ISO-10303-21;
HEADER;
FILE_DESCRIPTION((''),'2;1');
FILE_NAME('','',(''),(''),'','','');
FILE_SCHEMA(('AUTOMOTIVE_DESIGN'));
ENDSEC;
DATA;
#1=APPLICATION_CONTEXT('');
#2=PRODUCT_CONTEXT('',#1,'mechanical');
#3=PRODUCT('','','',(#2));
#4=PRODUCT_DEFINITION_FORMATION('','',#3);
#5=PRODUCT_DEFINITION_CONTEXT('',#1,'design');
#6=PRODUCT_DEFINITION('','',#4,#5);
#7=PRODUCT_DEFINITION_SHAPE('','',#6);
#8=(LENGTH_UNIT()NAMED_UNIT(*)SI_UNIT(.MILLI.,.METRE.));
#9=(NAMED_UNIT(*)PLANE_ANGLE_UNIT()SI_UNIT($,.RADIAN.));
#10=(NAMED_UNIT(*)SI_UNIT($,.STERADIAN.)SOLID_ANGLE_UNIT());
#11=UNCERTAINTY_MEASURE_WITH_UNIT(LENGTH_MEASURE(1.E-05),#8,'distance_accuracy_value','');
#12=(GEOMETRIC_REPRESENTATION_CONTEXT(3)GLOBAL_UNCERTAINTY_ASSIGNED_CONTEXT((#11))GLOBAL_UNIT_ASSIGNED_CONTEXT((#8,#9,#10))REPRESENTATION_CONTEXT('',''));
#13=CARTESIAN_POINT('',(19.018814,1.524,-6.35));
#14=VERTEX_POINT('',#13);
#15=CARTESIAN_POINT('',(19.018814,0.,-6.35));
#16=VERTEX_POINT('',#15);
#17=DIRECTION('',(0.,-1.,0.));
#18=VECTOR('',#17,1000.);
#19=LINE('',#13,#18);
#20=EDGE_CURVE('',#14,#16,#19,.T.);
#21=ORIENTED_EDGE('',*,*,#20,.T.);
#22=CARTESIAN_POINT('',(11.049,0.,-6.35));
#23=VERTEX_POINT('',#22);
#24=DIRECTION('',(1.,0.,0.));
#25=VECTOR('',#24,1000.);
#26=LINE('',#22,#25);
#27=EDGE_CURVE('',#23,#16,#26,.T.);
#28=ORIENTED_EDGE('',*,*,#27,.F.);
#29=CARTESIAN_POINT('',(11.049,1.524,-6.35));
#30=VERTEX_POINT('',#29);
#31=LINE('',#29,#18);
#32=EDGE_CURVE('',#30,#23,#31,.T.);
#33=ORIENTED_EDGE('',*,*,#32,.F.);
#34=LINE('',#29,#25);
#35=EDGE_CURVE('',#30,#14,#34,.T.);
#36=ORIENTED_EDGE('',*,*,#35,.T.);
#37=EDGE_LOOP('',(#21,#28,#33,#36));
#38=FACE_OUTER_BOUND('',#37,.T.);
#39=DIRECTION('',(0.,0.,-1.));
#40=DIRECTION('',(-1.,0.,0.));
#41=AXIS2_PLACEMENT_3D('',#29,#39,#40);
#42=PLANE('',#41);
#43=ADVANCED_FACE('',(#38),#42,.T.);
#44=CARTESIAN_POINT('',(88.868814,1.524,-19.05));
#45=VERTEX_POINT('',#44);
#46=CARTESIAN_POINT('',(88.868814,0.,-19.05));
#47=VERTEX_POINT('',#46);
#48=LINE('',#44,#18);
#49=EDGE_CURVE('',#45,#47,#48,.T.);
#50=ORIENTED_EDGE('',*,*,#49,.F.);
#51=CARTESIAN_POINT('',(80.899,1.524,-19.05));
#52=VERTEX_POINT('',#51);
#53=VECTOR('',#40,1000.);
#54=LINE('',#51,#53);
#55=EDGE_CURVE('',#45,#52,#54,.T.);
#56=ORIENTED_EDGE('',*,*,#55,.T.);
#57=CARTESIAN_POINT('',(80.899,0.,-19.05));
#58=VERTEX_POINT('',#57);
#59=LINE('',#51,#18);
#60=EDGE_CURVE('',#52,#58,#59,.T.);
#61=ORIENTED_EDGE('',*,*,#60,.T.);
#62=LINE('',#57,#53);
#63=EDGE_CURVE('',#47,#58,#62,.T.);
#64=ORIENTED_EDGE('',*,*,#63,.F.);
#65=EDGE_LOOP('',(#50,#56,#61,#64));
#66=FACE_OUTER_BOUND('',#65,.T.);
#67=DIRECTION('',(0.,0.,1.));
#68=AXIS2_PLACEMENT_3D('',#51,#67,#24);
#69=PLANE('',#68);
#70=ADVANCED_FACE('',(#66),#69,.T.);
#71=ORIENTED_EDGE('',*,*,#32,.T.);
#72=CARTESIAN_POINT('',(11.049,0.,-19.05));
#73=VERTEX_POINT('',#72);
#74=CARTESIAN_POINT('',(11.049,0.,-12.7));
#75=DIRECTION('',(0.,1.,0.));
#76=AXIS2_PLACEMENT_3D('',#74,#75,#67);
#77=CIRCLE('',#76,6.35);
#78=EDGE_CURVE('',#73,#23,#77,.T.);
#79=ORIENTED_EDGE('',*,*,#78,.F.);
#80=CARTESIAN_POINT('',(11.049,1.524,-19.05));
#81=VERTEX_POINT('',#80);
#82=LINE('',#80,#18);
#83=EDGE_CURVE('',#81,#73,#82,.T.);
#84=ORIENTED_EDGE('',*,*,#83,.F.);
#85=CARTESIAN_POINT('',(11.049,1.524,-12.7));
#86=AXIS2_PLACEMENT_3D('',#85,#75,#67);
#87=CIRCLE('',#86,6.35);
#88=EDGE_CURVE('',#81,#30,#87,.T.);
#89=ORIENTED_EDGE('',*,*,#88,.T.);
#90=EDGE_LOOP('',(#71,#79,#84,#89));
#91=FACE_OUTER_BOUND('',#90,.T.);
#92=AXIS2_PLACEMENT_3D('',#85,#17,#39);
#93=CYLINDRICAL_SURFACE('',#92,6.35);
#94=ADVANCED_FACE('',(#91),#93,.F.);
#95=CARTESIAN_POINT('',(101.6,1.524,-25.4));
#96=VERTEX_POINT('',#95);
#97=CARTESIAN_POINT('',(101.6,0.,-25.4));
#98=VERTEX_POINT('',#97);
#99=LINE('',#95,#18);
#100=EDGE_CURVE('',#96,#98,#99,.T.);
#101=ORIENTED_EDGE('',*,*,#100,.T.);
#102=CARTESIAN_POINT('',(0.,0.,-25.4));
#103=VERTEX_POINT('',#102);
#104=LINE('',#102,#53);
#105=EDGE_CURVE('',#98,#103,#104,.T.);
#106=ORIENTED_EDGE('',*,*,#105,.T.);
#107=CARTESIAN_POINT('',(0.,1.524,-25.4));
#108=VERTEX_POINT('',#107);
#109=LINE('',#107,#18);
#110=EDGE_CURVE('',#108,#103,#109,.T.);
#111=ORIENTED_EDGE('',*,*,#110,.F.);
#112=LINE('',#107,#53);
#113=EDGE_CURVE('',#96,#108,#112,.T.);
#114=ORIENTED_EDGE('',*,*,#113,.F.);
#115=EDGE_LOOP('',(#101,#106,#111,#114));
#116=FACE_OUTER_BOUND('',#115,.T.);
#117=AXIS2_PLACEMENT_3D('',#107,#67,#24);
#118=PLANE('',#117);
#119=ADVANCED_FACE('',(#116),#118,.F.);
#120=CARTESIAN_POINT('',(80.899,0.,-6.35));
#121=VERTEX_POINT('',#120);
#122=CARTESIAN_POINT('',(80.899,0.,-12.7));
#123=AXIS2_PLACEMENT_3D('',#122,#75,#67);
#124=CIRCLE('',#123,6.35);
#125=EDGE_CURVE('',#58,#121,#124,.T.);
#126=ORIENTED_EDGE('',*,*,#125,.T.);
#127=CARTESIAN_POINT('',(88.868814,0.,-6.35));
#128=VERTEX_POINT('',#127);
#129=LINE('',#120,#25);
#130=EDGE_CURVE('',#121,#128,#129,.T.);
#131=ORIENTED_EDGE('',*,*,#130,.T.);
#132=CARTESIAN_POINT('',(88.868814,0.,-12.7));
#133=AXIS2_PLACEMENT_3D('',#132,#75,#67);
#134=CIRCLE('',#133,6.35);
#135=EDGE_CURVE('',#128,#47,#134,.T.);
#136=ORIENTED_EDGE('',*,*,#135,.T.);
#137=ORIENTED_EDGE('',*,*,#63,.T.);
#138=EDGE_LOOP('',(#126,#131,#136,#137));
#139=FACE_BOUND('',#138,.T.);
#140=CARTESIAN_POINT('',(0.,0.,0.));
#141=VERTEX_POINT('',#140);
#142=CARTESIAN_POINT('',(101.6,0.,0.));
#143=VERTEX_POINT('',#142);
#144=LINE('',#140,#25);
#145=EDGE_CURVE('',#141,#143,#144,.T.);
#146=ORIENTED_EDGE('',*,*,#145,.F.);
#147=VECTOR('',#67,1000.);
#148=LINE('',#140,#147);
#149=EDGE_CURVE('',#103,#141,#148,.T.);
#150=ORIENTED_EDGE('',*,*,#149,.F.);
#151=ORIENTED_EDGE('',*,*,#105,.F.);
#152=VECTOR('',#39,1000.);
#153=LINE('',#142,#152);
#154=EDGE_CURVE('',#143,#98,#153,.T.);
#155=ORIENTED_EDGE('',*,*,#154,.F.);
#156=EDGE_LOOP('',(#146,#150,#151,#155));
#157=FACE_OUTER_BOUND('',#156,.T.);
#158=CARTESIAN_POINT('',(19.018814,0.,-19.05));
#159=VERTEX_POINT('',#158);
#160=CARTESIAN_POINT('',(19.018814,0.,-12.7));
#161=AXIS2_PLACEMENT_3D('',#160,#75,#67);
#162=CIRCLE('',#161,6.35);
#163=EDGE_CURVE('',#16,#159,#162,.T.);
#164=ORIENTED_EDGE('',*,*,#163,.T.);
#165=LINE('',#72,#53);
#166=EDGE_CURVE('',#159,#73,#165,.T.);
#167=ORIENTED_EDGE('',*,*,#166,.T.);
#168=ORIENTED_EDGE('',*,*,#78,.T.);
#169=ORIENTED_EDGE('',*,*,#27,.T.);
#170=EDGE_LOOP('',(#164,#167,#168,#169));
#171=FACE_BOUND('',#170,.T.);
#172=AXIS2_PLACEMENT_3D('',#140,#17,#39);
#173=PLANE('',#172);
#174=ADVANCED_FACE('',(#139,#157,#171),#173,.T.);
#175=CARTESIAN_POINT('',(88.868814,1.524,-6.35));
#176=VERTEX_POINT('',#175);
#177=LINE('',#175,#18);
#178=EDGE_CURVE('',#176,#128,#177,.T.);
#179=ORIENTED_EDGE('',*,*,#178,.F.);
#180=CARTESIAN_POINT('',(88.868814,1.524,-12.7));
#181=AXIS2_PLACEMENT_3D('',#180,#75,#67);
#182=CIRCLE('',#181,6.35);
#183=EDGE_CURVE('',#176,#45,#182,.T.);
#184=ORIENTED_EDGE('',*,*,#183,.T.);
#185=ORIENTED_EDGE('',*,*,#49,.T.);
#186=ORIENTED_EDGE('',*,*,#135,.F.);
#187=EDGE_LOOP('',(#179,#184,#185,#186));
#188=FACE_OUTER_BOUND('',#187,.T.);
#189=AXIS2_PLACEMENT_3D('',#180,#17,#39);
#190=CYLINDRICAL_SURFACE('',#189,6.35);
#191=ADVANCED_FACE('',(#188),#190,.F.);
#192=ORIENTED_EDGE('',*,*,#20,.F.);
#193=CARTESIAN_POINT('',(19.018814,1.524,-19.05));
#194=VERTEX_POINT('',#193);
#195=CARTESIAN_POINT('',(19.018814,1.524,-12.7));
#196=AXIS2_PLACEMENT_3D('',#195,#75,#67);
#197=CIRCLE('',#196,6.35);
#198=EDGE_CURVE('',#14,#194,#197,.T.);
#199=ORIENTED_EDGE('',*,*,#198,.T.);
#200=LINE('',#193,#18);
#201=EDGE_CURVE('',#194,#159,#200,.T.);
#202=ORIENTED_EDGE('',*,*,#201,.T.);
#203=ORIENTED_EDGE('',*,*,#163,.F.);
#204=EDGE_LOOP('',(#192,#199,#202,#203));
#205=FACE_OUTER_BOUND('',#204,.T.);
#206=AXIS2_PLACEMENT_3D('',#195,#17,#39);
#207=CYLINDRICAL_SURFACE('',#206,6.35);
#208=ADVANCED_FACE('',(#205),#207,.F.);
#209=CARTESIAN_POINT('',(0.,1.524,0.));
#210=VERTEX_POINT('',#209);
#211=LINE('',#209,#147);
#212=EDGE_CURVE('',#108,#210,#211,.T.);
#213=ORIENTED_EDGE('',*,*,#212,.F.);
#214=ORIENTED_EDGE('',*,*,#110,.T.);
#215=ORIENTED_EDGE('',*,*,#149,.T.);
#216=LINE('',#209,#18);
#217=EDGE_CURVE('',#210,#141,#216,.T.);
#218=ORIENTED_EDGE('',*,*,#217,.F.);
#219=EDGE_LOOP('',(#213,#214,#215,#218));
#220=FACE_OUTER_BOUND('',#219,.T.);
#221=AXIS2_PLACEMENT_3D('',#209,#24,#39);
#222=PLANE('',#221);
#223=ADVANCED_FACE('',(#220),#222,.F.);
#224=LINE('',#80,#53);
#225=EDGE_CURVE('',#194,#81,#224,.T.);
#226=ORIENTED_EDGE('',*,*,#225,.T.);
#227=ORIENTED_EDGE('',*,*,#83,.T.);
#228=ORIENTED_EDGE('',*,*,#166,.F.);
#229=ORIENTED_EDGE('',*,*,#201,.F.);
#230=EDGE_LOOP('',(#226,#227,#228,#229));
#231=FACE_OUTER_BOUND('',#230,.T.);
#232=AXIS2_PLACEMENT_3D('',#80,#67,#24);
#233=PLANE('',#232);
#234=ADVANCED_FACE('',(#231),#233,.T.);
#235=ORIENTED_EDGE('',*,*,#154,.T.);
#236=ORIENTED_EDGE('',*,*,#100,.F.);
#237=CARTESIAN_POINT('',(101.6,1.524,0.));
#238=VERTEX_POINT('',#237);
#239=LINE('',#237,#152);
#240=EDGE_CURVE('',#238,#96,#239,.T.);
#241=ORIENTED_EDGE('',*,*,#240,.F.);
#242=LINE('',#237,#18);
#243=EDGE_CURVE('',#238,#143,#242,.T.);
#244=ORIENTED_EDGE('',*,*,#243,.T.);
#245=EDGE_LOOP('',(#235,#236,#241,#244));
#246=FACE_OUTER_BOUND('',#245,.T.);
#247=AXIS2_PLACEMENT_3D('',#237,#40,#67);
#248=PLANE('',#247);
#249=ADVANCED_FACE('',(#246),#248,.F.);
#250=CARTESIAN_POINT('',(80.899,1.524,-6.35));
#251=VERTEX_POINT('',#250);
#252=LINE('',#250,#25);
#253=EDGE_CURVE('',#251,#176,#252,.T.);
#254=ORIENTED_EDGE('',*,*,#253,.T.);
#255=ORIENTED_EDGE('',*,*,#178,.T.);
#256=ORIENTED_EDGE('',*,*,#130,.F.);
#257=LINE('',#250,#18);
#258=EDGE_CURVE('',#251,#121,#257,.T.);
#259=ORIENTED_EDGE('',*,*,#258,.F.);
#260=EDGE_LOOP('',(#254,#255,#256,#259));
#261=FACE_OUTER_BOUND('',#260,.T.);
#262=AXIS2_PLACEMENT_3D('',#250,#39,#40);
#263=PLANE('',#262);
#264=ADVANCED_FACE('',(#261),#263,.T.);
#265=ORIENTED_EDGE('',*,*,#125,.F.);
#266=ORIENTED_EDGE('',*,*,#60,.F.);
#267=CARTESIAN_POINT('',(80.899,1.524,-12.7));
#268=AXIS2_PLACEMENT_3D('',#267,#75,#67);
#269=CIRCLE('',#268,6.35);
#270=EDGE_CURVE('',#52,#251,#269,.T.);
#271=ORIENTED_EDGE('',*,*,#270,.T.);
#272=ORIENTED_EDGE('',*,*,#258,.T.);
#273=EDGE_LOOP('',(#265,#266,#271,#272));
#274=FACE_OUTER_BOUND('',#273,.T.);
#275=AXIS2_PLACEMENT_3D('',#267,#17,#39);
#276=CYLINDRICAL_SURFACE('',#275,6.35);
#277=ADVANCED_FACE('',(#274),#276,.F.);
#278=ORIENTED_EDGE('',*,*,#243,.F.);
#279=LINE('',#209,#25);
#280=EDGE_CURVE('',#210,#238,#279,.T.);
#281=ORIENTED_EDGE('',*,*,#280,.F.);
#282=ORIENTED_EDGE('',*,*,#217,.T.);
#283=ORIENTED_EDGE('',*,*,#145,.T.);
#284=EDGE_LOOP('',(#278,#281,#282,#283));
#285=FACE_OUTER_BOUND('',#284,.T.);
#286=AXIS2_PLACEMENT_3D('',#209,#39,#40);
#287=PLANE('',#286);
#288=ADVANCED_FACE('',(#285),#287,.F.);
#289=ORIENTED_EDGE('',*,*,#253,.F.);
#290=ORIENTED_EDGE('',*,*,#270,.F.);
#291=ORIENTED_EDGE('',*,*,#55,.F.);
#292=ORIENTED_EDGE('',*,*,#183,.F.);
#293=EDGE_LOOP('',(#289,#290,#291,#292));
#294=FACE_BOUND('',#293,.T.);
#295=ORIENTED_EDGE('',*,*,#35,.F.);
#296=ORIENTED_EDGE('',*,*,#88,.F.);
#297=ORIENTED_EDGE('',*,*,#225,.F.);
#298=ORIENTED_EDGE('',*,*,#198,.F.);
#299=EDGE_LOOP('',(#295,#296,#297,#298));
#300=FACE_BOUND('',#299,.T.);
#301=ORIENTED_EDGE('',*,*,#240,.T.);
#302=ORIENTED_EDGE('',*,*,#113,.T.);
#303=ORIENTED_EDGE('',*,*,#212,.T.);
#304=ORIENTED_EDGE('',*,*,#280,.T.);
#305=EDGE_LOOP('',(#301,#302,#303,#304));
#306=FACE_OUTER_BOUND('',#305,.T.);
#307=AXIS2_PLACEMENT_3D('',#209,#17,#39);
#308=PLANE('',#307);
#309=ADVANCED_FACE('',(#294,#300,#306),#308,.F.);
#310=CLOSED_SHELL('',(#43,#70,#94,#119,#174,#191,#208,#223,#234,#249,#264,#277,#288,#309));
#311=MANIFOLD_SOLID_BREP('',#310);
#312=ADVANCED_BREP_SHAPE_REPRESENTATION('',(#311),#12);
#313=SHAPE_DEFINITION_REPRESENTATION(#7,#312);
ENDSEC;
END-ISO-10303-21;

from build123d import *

# Parameters (mm, degrees)
SKETCH1_W           = 101.6
SKETCH1_H           = 25.4
BOSS_EXTRUDE1_DEPTH = 1.524


with BuildPart() as part:
    # Sketch1 → Boss-Extrude1 (new body)
    with BuildSketch(Plane(origin=(0, 0, 0), x_dir=(1, 0, 0), z_dir=(0, 1, 0))):
        with Locations((50.8, 12.7)):
            Rectangle(SKETCH1_W, SKETCH1_H)
        with BuildLine():
            Line((11.049, 19.05), (19.018813647, 19.05))
            ThreePointArc((19.018813647, 19.05), (25.368813647, 12.7), (19.018813647, 6.35))
            Line((19.018813647, 6.35), (11.049, 6.35))
            ThreePointArc((11.049, 6.35), (4.699, 12.7), (11.049, 19.05))
        make_face(mode=Mode.SUBTRACT)
        with BuildLine():
            Line((80.899, 19.05), (88.868813647, 19.05))
            ThreePointArc((88.868813647, 19.05), (95.218813647, 12.7), (88.868813647, 6.35))
            Line((88.868813647, 6.35), (80.899, 6.35))
            ThreePointArc((80.899, 6.35), (74.549, 12.7), (80.899, 19.05))
        make_face(mode=Mode.SUBTRACT)
    extrude(amount=BOSS_EXTRUDE1_DEPTH)


solid = part.part
